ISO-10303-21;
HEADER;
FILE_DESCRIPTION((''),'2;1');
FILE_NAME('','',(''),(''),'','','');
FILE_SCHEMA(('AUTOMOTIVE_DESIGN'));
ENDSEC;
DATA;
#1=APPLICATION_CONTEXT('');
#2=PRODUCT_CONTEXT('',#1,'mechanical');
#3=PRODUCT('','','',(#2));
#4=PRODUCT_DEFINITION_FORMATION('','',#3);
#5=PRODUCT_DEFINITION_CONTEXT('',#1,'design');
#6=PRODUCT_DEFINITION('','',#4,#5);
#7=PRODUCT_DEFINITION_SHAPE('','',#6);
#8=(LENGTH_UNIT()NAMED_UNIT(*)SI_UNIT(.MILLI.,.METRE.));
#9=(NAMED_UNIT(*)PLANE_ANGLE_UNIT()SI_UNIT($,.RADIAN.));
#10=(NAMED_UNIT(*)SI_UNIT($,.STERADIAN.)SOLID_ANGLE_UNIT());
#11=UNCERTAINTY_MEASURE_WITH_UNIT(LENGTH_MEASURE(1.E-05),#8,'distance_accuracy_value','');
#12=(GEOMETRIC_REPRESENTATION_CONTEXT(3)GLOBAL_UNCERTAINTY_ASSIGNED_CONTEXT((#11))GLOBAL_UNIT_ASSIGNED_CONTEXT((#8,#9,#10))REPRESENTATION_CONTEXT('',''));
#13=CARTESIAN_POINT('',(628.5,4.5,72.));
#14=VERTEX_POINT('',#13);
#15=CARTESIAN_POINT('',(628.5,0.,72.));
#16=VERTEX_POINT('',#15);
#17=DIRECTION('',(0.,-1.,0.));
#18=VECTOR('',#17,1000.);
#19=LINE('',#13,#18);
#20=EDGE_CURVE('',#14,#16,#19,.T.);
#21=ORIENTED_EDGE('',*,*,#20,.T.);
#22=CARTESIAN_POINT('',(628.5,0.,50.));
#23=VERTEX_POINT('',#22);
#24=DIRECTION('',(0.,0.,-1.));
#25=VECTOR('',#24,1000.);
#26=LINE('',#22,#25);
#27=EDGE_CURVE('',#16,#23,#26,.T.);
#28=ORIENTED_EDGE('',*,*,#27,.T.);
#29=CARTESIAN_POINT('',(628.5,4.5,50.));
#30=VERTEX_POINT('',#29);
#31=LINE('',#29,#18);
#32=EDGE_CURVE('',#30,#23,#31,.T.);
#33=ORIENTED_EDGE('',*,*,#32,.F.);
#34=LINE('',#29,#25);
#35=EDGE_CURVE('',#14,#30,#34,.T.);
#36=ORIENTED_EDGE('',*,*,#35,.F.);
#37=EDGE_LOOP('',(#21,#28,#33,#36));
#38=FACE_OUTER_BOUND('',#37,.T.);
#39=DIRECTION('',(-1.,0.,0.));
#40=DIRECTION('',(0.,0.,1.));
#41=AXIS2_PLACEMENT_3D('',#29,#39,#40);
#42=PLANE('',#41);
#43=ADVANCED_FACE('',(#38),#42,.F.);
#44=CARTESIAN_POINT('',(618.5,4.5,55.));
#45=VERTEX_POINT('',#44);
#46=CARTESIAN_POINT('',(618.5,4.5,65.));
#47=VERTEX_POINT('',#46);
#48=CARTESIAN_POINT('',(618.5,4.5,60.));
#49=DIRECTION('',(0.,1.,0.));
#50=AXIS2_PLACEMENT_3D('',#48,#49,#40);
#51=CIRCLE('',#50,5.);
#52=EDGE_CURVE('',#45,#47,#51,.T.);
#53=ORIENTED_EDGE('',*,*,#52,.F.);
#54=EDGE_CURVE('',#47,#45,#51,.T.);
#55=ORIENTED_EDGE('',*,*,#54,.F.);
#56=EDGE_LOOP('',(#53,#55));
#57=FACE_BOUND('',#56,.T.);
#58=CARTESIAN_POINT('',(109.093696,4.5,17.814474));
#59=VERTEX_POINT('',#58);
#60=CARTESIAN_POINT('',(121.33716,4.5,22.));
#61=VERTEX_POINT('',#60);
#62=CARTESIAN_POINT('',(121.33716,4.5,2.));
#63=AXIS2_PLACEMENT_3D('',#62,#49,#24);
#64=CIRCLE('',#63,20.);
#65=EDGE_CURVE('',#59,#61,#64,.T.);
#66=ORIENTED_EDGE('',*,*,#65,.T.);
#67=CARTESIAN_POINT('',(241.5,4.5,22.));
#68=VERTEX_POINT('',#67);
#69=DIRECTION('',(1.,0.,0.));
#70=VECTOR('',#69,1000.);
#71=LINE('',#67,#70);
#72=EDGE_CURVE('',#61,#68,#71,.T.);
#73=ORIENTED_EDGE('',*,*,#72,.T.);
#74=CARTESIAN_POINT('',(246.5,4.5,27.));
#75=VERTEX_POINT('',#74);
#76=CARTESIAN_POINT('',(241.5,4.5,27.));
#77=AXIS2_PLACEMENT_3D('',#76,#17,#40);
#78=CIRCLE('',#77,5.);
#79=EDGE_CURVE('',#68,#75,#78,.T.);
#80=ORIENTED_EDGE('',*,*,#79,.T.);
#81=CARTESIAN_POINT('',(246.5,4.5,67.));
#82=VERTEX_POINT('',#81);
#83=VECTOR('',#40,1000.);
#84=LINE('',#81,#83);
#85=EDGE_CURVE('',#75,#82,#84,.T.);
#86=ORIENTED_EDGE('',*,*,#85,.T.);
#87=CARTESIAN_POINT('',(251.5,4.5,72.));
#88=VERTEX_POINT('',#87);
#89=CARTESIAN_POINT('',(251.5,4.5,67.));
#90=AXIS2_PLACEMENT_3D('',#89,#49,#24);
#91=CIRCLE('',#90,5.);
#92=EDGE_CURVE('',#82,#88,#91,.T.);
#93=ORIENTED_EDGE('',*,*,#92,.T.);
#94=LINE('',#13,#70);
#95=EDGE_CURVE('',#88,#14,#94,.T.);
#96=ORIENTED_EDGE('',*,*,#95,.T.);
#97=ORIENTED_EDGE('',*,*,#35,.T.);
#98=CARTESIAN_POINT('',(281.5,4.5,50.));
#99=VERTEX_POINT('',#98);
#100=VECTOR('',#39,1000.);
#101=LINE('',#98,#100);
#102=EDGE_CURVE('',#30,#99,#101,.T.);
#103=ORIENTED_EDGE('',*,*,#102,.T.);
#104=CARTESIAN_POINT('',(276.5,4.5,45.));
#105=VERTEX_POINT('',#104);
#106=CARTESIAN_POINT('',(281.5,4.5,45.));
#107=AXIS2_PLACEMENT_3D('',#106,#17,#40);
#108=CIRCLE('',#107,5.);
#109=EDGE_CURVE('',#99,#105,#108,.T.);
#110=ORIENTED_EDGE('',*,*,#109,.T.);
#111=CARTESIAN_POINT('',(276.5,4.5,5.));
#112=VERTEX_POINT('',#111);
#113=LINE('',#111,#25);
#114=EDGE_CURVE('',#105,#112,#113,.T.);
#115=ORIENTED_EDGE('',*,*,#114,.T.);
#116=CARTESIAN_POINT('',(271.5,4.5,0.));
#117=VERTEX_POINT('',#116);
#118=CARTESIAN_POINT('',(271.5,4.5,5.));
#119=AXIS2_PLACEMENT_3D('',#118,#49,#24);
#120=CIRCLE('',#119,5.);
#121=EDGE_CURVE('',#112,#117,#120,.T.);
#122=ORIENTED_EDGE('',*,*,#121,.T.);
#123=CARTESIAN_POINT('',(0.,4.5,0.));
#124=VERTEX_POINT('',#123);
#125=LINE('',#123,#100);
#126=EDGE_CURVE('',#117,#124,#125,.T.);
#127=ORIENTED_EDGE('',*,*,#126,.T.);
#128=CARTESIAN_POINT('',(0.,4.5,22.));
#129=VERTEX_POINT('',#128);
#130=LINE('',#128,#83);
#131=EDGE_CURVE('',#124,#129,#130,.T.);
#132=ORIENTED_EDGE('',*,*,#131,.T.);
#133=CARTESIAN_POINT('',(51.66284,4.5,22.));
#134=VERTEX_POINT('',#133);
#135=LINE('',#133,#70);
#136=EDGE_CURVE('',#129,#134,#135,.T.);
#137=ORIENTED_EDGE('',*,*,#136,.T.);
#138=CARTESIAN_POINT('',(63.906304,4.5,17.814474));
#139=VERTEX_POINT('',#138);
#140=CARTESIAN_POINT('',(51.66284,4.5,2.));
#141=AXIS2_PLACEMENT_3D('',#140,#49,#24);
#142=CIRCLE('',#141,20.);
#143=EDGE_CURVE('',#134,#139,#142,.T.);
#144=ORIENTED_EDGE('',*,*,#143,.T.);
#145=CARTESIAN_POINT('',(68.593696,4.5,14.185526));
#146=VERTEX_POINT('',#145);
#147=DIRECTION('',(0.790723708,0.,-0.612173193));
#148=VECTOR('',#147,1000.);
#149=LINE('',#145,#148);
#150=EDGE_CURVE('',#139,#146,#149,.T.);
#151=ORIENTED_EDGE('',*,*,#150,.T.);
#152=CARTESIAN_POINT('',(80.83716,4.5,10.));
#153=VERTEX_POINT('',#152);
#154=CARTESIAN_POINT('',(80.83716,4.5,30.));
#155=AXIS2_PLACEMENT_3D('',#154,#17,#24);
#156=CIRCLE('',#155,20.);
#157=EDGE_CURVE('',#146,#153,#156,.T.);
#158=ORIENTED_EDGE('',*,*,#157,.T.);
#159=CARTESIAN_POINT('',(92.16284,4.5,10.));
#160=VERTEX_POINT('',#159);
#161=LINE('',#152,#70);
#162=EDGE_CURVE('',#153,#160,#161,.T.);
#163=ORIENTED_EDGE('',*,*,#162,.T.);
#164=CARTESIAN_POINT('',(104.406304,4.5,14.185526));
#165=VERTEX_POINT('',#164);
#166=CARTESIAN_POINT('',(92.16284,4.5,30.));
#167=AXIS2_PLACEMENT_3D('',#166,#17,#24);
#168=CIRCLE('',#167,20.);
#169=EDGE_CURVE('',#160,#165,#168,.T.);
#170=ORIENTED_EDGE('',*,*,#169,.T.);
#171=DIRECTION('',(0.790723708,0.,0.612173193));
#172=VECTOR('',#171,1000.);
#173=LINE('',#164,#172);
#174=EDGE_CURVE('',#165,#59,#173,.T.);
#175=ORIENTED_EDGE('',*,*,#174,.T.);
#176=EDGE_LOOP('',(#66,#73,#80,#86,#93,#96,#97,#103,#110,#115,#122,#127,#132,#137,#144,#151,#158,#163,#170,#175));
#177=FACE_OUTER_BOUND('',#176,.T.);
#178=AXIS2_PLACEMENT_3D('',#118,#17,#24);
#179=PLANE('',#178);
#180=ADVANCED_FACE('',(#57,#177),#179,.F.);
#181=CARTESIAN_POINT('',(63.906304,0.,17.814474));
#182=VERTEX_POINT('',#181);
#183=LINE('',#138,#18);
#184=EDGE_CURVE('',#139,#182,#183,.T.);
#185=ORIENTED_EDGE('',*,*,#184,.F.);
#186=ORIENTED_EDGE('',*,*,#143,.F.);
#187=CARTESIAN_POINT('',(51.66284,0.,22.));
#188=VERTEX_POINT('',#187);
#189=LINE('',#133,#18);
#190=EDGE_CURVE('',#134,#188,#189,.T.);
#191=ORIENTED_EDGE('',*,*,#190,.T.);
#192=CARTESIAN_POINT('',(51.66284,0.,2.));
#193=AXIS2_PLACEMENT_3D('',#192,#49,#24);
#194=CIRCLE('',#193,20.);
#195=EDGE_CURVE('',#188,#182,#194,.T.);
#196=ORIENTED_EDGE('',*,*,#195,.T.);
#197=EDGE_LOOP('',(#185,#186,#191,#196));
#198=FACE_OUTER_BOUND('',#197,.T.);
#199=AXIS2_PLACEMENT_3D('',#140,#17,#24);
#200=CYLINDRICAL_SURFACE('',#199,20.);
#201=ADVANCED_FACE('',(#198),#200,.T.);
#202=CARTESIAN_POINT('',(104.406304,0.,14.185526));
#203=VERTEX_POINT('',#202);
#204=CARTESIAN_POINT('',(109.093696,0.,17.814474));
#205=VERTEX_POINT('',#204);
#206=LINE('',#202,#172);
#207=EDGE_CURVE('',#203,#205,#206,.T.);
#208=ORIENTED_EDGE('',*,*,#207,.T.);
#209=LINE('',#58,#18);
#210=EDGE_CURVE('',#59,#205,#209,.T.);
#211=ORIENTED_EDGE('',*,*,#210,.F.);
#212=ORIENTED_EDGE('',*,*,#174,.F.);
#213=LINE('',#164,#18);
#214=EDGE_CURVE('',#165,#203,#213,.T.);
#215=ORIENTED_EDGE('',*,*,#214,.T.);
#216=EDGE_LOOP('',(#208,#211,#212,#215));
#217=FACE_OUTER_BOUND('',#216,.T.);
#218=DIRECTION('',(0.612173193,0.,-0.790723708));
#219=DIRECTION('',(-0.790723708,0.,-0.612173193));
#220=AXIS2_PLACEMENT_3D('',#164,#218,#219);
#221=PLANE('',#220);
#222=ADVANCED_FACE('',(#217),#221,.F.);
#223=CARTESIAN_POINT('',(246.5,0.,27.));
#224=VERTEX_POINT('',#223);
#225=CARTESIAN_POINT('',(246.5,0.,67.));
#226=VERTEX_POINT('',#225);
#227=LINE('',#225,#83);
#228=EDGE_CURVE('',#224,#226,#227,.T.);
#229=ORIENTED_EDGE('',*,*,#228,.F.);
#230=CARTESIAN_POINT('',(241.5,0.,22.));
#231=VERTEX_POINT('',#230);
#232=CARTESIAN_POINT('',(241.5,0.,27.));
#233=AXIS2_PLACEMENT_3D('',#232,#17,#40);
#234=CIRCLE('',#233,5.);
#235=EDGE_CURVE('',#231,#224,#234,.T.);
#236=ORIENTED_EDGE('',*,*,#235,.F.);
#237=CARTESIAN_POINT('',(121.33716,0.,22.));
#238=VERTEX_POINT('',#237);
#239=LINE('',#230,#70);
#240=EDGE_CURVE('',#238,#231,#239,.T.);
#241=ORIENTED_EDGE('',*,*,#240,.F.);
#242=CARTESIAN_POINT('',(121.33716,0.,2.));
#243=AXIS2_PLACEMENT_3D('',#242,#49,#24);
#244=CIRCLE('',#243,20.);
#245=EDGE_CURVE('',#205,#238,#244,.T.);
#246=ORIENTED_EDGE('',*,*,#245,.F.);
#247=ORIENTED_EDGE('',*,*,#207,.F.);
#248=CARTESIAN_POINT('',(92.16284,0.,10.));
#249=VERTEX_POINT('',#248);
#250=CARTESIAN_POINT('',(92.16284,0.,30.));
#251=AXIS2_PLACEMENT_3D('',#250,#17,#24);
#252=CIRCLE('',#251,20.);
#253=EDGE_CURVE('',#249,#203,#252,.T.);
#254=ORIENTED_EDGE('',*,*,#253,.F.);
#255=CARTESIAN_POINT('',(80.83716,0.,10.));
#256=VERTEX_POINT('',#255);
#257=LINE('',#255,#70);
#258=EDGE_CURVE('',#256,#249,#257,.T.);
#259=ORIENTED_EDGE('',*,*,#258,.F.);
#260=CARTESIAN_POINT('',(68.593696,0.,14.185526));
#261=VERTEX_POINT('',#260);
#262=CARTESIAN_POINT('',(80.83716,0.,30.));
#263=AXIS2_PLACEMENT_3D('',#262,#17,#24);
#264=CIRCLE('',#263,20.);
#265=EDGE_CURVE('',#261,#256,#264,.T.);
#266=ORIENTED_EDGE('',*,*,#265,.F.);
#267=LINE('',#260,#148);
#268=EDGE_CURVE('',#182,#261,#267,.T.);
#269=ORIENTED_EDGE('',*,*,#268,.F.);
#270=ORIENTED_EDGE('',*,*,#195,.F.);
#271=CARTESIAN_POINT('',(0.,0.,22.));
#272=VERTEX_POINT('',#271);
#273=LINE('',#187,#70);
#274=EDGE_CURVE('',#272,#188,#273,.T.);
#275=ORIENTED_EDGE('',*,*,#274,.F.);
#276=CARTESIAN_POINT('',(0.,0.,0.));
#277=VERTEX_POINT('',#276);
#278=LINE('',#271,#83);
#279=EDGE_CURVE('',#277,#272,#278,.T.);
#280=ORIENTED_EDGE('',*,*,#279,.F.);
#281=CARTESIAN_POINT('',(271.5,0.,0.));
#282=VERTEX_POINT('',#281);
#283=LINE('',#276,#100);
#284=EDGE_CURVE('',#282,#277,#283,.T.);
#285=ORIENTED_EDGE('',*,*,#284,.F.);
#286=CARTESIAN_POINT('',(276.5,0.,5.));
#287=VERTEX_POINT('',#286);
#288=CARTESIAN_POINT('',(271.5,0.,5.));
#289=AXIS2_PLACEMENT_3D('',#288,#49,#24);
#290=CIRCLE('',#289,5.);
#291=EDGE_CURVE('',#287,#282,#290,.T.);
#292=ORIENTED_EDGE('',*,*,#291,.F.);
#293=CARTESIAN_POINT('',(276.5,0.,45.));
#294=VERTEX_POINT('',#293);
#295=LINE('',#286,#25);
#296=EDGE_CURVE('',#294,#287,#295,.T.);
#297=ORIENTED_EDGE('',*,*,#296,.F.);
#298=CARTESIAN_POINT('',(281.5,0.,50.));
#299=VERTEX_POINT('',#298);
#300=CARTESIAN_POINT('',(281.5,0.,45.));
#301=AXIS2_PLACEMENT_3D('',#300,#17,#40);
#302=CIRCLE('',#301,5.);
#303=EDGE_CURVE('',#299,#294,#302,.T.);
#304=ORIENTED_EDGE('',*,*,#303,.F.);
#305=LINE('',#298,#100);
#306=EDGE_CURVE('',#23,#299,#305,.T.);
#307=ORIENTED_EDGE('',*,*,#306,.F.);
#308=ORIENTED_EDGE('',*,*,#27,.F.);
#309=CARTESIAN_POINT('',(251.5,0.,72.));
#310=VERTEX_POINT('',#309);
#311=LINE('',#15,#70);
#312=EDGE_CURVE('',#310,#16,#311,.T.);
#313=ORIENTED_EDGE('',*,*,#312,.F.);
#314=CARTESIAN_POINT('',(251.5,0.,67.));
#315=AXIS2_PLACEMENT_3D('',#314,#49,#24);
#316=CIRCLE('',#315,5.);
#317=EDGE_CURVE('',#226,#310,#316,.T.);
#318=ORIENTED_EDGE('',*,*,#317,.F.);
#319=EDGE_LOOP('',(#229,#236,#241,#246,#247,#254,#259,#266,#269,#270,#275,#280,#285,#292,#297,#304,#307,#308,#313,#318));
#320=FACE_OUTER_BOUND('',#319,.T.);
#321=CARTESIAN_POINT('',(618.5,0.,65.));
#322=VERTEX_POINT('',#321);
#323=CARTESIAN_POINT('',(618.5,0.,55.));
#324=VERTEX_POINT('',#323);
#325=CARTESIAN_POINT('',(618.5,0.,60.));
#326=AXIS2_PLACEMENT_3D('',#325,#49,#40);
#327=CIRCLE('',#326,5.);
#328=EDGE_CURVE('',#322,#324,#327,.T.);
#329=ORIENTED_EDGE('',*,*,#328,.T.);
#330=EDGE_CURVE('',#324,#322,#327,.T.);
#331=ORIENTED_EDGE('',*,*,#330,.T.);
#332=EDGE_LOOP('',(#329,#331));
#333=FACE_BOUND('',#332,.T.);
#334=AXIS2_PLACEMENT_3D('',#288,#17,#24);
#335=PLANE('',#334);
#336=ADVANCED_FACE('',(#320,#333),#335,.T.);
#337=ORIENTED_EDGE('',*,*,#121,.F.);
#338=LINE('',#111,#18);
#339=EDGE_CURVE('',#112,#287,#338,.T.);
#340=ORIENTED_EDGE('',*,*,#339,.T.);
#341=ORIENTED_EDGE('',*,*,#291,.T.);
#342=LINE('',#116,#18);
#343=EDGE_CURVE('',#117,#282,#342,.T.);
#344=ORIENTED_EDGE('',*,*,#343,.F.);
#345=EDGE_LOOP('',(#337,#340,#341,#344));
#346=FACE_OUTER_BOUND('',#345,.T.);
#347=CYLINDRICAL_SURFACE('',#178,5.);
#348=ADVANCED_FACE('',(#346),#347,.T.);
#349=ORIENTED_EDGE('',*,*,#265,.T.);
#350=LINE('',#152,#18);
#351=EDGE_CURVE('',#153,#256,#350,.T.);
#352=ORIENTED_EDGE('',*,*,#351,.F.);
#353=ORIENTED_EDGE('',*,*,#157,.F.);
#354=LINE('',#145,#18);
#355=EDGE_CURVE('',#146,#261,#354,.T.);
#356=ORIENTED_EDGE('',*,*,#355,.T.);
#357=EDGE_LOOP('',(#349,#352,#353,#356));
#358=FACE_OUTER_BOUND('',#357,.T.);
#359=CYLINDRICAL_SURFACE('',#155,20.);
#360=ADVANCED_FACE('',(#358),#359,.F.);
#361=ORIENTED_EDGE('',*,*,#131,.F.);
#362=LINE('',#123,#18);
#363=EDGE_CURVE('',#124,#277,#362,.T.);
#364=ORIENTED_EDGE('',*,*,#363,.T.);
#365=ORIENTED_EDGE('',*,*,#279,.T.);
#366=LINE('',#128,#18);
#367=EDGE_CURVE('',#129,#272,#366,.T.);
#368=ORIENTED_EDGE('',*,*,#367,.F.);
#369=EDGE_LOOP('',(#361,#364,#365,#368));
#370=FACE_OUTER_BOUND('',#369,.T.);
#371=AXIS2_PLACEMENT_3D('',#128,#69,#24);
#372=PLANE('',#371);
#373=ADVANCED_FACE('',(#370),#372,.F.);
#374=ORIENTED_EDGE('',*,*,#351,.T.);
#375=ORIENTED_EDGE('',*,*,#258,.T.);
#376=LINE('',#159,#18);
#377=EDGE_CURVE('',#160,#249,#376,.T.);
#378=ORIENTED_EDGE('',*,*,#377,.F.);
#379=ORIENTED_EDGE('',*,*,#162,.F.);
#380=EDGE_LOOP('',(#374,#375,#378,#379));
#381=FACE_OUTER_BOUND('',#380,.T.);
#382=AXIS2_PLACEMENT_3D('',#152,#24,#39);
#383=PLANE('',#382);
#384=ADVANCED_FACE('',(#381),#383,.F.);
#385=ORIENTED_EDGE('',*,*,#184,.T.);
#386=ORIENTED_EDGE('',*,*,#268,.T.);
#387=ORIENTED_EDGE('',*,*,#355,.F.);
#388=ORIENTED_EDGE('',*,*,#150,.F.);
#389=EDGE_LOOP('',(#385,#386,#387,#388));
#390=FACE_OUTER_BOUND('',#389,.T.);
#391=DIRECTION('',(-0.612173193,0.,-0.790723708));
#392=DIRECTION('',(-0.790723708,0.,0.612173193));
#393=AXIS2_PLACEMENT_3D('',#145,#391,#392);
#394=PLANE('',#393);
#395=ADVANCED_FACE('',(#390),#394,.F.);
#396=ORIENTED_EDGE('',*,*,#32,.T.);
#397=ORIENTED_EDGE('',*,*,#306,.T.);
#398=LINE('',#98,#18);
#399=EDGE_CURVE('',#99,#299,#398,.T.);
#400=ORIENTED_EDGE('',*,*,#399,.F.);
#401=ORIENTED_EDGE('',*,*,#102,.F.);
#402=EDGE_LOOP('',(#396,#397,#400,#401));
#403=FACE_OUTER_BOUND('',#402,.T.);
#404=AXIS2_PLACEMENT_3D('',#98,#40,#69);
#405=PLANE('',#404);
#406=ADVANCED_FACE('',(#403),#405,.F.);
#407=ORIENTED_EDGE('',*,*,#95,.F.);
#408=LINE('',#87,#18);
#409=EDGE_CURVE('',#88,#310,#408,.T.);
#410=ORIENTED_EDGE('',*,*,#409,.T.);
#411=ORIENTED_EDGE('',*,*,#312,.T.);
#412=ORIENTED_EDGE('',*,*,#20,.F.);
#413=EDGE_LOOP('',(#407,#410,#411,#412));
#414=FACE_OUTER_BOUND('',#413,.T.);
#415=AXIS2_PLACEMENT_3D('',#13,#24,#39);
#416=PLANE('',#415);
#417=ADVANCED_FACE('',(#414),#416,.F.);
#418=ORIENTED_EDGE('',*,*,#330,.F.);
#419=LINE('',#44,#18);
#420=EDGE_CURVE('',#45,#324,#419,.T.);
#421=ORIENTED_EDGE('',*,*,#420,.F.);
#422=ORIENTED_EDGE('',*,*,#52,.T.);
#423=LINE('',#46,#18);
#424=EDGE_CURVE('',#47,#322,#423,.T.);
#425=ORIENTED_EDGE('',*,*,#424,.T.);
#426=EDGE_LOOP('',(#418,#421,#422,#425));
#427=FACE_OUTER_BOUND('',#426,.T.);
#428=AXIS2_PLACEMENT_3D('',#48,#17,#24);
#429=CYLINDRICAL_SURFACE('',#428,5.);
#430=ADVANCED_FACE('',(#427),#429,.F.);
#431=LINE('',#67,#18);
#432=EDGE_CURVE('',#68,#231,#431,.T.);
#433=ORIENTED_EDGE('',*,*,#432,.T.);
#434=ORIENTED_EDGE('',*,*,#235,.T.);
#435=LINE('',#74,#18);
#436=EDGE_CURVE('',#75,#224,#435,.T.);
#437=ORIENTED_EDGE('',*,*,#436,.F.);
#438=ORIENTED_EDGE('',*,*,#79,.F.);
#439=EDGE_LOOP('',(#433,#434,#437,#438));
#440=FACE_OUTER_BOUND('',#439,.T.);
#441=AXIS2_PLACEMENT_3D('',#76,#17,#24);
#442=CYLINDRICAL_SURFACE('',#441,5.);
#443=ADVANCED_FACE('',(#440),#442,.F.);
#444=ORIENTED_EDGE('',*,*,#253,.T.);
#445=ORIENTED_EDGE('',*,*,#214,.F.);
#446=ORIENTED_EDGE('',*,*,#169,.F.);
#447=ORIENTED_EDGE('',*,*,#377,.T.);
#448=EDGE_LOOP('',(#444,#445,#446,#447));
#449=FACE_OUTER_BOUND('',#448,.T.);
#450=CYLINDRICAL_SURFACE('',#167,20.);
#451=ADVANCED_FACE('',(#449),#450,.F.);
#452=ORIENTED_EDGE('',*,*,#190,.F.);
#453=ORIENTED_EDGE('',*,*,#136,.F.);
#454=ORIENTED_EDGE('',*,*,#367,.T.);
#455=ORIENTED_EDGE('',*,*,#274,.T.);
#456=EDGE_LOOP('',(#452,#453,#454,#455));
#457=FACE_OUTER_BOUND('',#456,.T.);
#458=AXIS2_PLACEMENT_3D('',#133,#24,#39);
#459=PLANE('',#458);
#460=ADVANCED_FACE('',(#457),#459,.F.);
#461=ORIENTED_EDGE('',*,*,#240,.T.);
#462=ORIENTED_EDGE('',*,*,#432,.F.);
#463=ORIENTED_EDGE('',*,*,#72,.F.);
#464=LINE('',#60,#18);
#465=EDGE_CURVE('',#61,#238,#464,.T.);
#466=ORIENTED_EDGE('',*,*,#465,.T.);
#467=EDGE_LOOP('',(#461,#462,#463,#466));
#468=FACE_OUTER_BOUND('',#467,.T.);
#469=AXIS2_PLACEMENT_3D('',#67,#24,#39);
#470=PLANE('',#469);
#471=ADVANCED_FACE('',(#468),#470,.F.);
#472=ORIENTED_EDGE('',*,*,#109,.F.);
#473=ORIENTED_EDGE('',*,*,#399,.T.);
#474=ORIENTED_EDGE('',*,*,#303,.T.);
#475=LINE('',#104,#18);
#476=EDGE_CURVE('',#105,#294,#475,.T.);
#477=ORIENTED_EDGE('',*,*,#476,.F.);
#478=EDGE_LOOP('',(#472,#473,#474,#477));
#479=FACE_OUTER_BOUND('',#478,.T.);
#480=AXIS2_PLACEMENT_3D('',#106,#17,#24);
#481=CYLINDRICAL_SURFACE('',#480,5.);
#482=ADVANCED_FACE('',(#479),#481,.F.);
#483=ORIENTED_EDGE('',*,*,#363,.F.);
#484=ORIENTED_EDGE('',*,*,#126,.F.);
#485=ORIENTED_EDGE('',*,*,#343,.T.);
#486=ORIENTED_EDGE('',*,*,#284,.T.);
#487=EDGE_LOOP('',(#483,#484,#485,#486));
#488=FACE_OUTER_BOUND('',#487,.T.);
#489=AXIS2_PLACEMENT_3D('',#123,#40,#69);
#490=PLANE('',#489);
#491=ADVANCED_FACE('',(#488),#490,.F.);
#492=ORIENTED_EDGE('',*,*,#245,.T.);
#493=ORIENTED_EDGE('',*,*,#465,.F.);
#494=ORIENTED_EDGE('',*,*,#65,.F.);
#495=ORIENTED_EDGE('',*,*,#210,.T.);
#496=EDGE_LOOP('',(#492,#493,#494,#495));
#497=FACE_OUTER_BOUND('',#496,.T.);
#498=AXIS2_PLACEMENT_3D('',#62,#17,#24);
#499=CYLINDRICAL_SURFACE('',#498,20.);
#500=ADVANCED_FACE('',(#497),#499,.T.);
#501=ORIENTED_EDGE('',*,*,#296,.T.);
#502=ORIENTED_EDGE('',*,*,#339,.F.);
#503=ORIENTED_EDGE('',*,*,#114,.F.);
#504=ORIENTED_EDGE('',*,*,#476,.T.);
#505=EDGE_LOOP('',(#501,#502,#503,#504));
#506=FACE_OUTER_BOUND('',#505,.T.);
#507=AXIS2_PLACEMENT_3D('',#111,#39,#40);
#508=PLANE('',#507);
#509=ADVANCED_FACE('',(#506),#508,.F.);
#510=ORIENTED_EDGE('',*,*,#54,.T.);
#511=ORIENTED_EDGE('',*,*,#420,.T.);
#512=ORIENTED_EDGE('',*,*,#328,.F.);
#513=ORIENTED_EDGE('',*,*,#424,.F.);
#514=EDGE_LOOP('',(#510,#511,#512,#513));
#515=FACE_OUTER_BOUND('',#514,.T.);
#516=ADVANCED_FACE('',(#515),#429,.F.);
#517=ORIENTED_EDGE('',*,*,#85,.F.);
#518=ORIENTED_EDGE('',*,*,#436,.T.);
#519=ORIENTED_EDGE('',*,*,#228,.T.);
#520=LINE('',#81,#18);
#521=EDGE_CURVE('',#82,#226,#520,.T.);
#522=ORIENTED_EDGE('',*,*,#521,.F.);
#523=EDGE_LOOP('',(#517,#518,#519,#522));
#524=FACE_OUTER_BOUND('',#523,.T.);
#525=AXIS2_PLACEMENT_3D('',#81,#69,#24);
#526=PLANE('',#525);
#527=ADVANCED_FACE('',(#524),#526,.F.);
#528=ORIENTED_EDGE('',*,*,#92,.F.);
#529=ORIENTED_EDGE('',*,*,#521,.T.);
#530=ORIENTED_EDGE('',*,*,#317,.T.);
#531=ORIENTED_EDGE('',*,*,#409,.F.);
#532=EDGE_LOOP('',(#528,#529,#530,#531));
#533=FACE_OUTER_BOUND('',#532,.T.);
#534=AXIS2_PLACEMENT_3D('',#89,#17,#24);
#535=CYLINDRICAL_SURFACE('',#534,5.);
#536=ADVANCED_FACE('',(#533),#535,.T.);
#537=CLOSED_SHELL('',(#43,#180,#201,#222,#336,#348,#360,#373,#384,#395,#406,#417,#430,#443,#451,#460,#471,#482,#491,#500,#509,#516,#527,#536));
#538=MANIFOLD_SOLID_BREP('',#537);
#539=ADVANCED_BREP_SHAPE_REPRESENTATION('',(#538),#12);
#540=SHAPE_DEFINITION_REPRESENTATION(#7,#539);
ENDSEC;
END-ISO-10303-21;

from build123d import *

# Parameters (mm, degrees)
SKETCH1_R           = 5
BOSS_EXTRUDE1_DEPTH = 4.5


with BuildPart() as part:
    # Sketch1 → Boss-Extrude1 (new body)
    with BuildSketch(Plane(origin=(0, 0, 0), x_dir=(1, 0, 0), z_dir=(0, 1, 0))):
        with BuildLine():
            Line((0, 0), (271.5, 0))
            ThreePointArc((271.5, 0), (275.035533906, -1.464466094), (276.5, -5))
            Line((276.5, -5), (276.5, -45))
            ThreePointArc((276.5, -45), (277.964466094, -48.535533906), (281.5, -50))
            Line((281.5, -50), (628.5, -50))
            Line((628.5, -50), (628.5, -72))
            Line((628.5, -72), (251.5, -72))
            ThreePointArc((251.5, -72), (247.964466094, -70.535533906), (246.5, -67))
            Line((246.5, -67), (246.5, -27))
            ThreePointArc((246.5, -27), (245.035533906, -23.464466094), (241.5, -22))
            Line((241.5, -22), (121.33715964, -22))
            ThreePointArc((121.33715964, -22), (114.86759563, -20.924712455), (109.09369578, -17.814474152))
            Line((109.09369578, -17.814474152), (104.40630422, -14.185525848))
            ThreePointArc((104.40630422, -14.185525848), (98.63240437, -11.075287545), (92.16284036, -10))
            Line((92.16284036, -10), (80.83715964, -10))
            ThreePointArc((80.83715964, -10), (74.36759563, -11.075287545), (68.59369578, -14.185525848))
            Line((68.59369578, -14.185525848), (63.90630422, -17.814474152))
            ThreePointArc((63.90630422, -17.814474152), (58.13240437, -20.924712455), (51.66284036, -22))
            Line((51.66284036, -22), (0, -22))
            Line((0, -22), (0, 0))
        make_face()
        with Locations(Location((618.5, -60, 0), (0, 0, 270))):
            Circle(SKETCH1_R, mode=Mode.SUBTRACT)
    extrude(amount=BOSS_EXTRUDE1_DEPTH)


solid = part.part
